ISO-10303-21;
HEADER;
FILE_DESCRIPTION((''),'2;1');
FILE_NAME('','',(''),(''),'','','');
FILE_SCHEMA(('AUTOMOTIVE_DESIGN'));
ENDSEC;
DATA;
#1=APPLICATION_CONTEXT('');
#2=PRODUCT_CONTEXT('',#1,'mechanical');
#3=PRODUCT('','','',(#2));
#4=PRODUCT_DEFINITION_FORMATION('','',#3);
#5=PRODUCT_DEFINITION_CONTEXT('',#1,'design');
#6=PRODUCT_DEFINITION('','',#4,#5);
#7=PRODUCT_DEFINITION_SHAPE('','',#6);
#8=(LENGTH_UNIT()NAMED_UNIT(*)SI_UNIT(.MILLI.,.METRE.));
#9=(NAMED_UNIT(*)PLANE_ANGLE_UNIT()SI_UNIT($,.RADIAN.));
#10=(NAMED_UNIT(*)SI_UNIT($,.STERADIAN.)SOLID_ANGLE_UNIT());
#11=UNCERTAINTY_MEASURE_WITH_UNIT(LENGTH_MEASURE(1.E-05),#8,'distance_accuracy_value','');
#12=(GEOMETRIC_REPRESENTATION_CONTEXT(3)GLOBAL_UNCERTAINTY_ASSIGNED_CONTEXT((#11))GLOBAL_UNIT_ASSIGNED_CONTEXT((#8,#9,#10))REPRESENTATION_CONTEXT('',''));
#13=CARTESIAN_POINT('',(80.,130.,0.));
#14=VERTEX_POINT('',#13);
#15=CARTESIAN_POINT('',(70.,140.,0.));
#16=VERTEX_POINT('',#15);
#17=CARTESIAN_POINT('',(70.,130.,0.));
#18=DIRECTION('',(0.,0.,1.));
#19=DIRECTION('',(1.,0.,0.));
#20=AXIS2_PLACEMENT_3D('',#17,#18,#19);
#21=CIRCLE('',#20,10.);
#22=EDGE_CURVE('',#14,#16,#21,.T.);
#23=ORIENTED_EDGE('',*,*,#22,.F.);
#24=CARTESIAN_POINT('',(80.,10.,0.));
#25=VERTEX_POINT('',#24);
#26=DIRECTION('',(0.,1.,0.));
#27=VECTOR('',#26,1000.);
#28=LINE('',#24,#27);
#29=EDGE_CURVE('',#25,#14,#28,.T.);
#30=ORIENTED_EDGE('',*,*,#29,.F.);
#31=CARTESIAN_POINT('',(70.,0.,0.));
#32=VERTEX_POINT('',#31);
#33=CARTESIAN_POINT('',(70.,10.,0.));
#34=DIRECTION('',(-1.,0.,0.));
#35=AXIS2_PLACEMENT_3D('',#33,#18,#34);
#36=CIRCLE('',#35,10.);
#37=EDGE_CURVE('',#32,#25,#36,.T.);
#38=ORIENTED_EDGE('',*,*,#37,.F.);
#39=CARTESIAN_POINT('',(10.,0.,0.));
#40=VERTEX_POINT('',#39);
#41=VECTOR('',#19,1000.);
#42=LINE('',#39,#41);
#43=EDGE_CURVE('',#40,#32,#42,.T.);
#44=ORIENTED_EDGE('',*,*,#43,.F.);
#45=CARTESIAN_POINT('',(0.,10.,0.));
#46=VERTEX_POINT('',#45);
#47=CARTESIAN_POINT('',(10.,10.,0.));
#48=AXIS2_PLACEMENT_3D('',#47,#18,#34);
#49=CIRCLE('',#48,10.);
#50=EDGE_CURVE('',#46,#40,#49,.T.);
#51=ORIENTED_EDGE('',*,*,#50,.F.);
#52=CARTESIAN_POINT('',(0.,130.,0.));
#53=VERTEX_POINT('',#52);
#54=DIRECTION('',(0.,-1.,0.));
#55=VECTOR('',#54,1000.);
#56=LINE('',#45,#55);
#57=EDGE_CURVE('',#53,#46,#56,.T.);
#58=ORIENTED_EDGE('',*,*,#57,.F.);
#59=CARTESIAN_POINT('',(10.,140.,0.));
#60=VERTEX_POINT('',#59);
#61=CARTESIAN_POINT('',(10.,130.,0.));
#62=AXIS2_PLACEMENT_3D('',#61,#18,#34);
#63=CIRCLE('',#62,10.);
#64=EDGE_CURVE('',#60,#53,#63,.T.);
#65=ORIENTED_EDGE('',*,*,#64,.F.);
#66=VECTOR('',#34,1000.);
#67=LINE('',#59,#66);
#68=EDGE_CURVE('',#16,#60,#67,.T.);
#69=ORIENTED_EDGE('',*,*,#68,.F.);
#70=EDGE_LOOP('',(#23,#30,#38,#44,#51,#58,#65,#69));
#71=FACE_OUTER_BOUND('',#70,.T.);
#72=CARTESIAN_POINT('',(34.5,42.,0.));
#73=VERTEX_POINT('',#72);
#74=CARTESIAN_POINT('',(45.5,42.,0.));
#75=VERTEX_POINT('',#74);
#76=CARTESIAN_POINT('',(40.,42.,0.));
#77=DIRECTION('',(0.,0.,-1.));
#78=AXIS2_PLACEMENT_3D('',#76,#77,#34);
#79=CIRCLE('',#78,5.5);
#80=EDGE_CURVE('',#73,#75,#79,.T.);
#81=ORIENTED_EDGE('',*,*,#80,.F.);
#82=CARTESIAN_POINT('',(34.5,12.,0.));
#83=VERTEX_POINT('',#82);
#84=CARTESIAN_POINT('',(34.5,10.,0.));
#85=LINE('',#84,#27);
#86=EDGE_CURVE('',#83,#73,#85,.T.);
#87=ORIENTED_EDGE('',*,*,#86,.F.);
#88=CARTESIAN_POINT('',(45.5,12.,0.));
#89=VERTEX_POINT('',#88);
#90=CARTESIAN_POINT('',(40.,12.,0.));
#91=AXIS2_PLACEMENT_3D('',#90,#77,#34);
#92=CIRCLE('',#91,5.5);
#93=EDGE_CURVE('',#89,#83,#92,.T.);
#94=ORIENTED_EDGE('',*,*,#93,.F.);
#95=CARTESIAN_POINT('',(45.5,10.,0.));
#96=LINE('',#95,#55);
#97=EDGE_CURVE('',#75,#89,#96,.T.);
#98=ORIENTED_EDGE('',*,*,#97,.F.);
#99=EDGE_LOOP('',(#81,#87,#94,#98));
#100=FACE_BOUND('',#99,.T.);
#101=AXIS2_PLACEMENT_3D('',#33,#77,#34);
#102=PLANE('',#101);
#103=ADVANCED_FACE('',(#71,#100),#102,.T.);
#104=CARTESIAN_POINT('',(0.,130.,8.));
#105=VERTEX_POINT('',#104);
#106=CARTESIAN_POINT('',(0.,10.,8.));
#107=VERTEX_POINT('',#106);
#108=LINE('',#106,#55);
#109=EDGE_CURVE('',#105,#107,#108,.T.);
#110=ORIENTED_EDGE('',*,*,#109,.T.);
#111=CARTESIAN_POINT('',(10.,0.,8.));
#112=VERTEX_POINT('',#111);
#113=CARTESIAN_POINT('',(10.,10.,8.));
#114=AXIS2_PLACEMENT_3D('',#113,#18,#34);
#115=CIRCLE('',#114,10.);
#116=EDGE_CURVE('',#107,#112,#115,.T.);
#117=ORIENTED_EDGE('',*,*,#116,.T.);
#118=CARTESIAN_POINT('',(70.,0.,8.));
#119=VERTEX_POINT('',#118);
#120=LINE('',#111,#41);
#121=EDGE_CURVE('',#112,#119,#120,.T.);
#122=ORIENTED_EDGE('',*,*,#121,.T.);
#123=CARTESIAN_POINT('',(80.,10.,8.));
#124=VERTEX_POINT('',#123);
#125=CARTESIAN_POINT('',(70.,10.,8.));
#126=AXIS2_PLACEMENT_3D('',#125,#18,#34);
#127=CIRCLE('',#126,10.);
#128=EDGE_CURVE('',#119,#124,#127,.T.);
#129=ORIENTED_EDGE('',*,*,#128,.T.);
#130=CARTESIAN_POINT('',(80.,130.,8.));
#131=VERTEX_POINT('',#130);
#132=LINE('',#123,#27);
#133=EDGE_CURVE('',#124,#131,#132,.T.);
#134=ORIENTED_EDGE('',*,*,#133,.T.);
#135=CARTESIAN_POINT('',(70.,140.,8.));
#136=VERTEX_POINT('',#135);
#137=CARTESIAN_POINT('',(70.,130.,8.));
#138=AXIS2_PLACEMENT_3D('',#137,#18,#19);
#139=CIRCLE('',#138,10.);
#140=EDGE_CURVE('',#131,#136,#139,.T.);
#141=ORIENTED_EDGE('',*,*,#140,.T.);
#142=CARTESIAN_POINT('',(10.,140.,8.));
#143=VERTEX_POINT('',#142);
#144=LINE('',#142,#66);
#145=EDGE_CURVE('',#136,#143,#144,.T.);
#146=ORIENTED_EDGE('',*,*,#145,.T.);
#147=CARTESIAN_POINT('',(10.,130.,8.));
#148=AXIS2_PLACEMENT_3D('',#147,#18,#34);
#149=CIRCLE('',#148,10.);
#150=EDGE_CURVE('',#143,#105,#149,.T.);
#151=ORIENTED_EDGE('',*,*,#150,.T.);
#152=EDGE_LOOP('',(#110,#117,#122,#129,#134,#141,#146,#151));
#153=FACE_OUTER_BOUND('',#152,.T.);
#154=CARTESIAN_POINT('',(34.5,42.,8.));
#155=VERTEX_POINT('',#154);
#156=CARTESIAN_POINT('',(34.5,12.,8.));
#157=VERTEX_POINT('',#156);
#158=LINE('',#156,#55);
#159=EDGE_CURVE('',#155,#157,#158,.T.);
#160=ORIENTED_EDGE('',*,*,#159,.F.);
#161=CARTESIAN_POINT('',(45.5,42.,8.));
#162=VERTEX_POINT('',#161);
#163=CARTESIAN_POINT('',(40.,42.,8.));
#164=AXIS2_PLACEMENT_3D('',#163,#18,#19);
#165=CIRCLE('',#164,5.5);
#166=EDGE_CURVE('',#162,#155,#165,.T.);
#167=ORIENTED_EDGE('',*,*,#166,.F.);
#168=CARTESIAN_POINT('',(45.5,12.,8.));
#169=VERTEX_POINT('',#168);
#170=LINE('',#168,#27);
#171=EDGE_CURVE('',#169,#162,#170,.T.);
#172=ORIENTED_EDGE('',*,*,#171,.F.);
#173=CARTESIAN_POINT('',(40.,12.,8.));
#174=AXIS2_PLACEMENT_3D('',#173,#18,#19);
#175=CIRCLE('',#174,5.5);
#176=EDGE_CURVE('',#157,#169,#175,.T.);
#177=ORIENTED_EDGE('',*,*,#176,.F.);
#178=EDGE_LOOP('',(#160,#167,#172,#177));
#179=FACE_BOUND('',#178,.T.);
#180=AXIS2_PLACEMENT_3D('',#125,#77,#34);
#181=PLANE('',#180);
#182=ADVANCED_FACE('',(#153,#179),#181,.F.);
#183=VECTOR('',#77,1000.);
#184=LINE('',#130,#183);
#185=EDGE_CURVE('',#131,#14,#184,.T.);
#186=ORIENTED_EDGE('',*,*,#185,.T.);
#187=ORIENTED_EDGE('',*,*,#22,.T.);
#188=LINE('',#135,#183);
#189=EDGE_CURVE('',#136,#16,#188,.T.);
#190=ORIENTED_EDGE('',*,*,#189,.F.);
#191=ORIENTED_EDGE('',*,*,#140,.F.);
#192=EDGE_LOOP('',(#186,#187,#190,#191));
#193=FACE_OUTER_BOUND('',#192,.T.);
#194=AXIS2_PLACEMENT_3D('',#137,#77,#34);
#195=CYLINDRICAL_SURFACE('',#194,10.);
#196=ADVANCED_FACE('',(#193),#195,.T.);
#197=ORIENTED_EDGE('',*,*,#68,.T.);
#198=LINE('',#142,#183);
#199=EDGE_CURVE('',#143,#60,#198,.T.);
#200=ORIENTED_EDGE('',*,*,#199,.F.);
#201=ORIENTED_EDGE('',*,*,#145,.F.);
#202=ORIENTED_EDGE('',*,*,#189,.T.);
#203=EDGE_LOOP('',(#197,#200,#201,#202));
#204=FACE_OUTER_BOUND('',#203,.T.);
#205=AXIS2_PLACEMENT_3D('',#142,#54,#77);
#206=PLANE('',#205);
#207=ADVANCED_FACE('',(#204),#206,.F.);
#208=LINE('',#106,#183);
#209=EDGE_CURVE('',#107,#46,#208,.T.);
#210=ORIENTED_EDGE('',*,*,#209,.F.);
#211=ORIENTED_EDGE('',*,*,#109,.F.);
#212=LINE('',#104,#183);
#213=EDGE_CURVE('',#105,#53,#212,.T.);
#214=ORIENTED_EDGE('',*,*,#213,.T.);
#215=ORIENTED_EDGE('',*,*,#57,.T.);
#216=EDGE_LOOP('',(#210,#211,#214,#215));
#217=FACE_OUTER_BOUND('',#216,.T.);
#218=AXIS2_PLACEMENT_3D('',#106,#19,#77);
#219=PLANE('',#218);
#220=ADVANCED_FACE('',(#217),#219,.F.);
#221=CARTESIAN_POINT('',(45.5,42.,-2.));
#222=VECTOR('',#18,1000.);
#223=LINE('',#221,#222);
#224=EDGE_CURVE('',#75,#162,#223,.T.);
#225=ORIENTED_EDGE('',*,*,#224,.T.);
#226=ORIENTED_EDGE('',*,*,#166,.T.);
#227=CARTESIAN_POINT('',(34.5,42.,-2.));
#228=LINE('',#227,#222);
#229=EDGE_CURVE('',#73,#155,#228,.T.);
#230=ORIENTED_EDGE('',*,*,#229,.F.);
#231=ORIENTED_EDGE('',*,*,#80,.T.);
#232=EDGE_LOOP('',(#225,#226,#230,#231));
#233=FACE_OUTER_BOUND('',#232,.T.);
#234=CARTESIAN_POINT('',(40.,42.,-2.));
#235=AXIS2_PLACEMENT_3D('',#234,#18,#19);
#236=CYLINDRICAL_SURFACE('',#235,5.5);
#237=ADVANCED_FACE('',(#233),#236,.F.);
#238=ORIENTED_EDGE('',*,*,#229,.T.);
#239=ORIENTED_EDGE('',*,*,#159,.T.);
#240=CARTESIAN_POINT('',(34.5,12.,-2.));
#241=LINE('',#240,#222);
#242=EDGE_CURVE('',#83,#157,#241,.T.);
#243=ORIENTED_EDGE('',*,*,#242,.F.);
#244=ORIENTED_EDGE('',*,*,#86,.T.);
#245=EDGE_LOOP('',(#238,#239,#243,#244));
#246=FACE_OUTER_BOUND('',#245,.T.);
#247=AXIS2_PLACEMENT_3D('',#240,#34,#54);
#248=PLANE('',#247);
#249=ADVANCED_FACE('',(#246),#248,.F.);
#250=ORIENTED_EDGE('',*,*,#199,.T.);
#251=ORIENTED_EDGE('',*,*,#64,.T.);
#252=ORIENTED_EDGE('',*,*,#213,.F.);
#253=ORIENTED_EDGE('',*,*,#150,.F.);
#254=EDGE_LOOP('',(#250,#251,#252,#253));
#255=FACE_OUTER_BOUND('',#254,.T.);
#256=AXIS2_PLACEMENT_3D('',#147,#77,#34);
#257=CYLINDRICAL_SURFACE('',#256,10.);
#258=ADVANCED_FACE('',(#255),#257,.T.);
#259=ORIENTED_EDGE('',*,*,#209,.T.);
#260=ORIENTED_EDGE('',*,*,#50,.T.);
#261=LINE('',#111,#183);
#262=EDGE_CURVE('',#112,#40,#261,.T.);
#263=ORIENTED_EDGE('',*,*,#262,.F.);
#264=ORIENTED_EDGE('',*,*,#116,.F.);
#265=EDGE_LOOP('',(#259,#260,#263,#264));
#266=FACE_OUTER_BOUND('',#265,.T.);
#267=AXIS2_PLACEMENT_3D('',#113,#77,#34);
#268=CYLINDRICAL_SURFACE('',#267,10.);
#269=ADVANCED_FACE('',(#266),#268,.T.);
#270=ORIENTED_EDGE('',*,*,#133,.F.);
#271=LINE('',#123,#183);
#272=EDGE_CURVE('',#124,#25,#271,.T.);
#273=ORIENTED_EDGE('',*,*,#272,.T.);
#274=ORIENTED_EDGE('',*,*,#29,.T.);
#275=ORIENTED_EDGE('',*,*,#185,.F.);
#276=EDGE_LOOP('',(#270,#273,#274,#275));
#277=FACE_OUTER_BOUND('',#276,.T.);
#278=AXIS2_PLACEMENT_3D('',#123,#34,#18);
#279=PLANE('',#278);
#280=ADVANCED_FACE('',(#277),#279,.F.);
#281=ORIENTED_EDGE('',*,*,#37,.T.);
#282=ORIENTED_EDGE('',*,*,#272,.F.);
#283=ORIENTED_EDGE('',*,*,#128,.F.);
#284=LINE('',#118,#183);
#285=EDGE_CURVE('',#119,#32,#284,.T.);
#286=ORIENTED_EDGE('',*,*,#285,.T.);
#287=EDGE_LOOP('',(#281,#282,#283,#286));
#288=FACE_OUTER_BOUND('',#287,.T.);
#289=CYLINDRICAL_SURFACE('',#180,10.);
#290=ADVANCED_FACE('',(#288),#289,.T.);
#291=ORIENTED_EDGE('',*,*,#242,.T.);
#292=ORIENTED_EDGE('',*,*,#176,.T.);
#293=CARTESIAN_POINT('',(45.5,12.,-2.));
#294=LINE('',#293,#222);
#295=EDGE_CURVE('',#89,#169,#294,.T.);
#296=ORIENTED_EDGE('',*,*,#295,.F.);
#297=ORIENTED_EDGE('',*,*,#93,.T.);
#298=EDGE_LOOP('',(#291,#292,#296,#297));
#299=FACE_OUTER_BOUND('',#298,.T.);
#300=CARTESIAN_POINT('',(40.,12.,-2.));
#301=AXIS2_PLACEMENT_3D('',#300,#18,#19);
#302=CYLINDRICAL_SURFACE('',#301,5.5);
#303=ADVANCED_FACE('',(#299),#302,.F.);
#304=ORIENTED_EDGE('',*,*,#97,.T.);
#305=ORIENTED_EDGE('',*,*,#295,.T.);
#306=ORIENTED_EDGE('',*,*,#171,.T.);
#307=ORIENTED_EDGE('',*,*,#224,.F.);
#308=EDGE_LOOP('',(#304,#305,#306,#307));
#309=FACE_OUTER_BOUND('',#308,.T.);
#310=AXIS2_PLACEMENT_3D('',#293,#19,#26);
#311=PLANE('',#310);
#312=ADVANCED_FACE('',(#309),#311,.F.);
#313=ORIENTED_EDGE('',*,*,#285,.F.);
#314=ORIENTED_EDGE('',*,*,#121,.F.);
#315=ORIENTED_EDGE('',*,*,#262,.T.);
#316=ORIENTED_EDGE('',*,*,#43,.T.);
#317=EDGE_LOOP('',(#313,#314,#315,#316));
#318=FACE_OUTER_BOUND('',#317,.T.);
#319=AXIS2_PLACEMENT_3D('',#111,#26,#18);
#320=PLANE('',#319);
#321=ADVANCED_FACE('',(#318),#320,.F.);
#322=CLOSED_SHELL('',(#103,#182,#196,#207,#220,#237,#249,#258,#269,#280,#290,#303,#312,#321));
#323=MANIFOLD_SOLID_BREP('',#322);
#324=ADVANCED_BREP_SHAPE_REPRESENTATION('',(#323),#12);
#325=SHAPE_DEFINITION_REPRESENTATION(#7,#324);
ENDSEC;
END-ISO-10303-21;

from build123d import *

# Parameters (mm, degrees)
BOSS_EXTRUDE1_DEPTH = 8
CUT_EXTRUDE1_DEPTH  = 10


with BuildPart() as part:
    # Sketch1 → Boss-Extrude1 (new body)
    with BuildSketch(Plane.XY):
        with BuildLine():
            Line((10, 0), (70, 0))
            ThreePointArc((70, 0), (77.071067812, 2.928932188), (80, 10))
            Line((80, 10), (80, 130))
            ThreePointArc((80, 130), (77.071067812, 137.071067812), (70, 140))
            Line((70, 140), (10, 140))
            ThreePointArc((10, 140), (2.928932188, 137.071067812), (0, 130))
            Line((0, 130), (0, 10))
            ThreePointArc((0, 10), (2.928932188, 2.928932188), (10, 0))
        make_face()
    extrude(amount=BOSS_EXTRUDE1_DEPTH)

    # Sketch2 → Cut-Extrude1 (cut)
    with BuildSketch(Plane.XY.offset(8)):
        with BuildLine():
            Line((34.5, 12), (34.5, 42))
            ThreePointArc((34.5, 42), (40, 47.5), (45.5, 42))
            Line((45.5, 42), (45.5, 12))
            ThreePointArc((45.5, 12), (40, 6.5), (34.5, 12))
        make_face()
    extrude(amount=-CUT_EXTRUDE1_DEPTH, mode=Mode.SUBTRACT)


solid = part.part
